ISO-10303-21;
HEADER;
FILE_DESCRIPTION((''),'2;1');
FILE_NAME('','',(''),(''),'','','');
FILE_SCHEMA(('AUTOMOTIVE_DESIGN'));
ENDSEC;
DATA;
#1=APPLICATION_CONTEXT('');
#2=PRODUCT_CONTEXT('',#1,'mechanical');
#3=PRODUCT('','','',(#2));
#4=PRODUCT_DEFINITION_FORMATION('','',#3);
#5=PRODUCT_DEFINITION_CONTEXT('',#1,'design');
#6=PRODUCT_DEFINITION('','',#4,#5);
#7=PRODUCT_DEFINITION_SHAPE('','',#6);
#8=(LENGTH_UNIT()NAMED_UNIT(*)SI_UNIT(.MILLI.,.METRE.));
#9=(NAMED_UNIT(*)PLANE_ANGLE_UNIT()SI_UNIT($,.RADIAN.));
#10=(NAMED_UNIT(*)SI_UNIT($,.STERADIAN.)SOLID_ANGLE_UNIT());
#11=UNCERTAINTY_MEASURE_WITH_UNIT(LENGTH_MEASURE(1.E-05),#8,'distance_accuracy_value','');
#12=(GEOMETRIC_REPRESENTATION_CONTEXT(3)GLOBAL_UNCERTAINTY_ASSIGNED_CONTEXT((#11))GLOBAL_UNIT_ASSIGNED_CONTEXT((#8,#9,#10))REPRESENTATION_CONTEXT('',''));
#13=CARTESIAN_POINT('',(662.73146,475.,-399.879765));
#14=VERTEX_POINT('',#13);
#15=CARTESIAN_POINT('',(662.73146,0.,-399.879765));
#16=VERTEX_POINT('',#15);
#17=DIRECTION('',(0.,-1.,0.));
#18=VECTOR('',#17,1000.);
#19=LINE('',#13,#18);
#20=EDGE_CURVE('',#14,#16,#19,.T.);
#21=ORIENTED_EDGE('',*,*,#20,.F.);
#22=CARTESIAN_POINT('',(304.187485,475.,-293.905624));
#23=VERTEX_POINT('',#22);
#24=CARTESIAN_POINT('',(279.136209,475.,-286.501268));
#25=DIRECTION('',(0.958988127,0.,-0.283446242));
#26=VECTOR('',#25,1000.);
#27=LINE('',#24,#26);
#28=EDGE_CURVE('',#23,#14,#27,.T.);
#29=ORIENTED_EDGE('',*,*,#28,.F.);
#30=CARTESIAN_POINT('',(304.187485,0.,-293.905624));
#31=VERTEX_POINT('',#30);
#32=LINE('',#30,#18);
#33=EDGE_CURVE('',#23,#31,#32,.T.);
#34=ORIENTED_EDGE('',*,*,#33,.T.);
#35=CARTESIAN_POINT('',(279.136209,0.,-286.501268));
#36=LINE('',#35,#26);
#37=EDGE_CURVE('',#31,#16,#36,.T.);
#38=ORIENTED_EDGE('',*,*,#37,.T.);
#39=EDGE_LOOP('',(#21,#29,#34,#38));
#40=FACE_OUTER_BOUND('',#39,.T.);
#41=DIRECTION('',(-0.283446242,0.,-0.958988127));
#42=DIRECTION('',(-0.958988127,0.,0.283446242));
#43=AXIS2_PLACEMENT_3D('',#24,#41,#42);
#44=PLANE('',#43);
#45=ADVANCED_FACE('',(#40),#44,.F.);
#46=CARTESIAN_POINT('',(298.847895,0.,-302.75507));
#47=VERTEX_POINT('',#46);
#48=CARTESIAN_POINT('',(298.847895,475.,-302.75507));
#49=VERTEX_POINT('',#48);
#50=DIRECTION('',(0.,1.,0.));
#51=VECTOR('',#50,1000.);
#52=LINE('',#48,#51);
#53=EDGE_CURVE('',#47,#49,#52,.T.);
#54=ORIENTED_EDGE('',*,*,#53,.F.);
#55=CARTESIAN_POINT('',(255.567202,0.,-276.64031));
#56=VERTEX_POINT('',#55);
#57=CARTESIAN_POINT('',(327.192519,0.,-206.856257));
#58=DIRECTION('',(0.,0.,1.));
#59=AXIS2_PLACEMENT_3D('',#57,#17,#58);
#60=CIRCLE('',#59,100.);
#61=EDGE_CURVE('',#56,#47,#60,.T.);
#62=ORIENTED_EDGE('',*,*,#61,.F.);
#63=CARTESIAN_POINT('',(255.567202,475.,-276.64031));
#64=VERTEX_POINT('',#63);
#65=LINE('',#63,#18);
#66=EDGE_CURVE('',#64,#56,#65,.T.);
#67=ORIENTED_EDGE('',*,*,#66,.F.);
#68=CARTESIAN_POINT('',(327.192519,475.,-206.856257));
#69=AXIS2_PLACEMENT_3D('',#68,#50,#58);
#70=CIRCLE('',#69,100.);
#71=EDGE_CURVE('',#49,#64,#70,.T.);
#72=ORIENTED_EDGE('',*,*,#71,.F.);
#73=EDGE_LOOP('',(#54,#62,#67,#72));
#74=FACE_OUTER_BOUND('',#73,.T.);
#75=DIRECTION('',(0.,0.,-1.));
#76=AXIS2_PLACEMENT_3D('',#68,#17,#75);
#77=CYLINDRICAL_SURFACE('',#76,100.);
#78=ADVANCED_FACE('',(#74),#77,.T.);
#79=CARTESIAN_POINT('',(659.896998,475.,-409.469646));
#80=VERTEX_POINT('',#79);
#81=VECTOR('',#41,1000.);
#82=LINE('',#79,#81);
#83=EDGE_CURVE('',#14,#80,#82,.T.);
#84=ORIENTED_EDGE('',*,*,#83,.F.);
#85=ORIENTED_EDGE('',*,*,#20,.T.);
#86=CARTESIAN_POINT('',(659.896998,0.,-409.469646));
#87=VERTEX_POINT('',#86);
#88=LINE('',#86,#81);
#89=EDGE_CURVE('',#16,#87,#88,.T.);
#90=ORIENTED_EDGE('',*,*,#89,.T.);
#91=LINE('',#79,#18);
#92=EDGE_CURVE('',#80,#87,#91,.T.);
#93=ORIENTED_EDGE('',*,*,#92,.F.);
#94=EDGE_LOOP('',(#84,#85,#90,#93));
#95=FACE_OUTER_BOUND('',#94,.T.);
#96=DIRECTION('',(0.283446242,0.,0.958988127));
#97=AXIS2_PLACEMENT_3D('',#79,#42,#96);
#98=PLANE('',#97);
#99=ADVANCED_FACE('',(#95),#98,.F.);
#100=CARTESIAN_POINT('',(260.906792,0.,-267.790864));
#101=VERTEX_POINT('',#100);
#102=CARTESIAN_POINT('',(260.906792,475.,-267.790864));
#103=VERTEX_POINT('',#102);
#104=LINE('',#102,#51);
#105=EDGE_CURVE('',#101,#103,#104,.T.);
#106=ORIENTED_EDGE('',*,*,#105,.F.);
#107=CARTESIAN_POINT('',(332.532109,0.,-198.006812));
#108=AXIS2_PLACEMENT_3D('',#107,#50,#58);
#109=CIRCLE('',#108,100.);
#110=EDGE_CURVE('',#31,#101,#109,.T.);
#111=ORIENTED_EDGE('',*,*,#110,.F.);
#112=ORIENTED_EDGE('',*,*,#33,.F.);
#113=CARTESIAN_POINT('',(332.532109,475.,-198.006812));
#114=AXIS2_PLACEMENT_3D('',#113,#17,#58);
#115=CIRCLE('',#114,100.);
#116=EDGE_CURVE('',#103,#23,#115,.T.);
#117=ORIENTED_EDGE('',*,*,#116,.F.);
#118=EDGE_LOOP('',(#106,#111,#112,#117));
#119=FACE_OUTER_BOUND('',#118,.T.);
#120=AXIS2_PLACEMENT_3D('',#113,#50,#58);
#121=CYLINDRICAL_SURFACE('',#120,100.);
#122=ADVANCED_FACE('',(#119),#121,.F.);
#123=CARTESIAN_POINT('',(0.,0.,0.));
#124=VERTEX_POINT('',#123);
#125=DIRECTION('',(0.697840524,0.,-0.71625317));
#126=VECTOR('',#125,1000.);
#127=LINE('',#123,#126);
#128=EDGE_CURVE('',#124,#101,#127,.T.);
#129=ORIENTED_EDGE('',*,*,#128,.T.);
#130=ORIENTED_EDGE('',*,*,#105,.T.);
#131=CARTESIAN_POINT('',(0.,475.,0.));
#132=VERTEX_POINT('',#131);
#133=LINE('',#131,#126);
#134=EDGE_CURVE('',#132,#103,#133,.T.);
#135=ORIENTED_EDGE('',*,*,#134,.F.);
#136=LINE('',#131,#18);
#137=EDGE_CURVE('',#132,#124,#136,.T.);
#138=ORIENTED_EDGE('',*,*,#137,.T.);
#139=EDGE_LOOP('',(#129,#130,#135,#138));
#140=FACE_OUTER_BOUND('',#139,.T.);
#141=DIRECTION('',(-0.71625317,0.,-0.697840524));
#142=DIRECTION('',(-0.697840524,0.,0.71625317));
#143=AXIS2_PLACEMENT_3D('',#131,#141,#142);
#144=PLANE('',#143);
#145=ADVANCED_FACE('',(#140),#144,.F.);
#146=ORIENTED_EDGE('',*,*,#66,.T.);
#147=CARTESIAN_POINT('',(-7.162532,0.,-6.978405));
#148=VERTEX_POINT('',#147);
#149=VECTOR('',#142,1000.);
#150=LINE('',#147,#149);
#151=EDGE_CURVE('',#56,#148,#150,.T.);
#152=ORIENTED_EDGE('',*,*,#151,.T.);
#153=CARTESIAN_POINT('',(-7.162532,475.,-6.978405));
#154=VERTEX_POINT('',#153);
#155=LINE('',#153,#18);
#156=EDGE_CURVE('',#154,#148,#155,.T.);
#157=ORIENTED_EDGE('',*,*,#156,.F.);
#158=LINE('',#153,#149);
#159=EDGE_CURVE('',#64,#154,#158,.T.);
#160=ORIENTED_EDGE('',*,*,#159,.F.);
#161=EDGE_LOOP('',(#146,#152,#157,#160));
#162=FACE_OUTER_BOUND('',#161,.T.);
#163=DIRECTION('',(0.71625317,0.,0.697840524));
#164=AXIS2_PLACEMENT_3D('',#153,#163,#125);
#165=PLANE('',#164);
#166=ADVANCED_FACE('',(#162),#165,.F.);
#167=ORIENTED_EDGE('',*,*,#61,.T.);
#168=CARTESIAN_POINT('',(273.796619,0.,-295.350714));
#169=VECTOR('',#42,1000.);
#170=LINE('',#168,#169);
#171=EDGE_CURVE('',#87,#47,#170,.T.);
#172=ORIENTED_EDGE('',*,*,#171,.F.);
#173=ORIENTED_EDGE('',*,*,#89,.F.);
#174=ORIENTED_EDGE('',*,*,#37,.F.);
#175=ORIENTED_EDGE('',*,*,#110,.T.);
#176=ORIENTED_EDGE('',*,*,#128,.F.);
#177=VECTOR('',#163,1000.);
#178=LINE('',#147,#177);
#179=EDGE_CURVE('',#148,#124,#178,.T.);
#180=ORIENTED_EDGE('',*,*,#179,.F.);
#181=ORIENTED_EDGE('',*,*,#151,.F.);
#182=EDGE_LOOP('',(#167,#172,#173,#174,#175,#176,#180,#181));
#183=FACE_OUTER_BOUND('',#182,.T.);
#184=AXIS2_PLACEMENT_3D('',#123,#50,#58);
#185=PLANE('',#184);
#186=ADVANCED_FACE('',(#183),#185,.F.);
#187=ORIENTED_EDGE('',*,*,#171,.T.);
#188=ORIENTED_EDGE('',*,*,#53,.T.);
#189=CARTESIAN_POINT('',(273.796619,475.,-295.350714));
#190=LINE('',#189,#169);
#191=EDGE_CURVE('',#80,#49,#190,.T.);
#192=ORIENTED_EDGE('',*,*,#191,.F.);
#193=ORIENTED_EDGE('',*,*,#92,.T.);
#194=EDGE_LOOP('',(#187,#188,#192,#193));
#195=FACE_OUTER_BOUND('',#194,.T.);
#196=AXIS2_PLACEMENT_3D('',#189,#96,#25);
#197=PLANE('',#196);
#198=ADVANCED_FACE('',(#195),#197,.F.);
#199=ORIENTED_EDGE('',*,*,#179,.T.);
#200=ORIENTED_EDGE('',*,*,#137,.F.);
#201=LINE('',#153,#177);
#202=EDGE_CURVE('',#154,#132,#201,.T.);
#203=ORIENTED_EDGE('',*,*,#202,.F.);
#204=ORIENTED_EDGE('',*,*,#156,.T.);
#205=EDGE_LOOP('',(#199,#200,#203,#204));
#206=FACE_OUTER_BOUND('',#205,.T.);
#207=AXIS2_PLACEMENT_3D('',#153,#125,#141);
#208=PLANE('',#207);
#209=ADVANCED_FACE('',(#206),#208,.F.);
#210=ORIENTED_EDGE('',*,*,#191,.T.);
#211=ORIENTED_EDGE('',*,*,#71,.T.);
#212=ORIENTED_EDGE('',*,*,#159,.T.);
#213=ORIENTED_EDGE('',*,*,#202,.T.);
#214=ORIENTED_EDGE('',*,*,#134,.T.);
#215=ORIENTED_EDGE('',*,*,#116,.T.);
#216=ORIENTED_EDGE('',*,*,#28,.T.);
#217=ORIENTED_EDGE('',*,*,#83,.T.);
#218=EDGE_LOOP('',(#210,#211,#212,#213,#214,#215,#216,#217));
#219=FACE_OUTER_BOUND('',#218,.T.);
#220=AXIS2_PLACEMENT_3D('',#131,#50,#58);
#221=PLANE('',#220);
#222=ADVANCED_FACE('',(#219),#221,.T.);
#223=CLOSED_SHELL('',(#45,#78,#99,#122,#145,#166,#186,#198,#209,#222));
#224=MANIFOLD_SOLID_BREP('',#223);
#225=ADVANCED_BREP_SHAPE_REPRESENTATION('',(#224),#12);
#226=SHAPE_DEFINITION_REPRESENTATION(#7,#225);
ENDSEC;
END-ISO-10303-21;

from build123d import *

# Parameters (mm, degrees)
BOSS_EXTRUDE1_DEPTH = 475
FILLET1_R           = 100


with BuildPart() as part:
    # Sketch1 → Boss-Extrude1 (new body)
    with BuildSketch(Plane(origin=(0, 0, 0), x_dir=(1, 0, 0), z_dir=(0, 1, 0))):
        Polygon((0, 0), (279.136209435, 286.501268029), (662.731460294, 399.879764751), (659.896997876, 409.469646022), (273.796619493, 295.350713666), (-7.162531701, 6.978405236), align=None)
    extrude(amount=BOSS_EXTRUDE1_DEPTH)

    # Fillet1
    fillet1_edges = [part.edges().sort_by_distance(p)[0] for p in [
        (273.796619493, 237.5, -295.350713666),
        (279.136209435, 237.5, -286.501268029),
    ]]
    fillet(fillet1_edges, radius=FILLET1_R)


solid = part.part
